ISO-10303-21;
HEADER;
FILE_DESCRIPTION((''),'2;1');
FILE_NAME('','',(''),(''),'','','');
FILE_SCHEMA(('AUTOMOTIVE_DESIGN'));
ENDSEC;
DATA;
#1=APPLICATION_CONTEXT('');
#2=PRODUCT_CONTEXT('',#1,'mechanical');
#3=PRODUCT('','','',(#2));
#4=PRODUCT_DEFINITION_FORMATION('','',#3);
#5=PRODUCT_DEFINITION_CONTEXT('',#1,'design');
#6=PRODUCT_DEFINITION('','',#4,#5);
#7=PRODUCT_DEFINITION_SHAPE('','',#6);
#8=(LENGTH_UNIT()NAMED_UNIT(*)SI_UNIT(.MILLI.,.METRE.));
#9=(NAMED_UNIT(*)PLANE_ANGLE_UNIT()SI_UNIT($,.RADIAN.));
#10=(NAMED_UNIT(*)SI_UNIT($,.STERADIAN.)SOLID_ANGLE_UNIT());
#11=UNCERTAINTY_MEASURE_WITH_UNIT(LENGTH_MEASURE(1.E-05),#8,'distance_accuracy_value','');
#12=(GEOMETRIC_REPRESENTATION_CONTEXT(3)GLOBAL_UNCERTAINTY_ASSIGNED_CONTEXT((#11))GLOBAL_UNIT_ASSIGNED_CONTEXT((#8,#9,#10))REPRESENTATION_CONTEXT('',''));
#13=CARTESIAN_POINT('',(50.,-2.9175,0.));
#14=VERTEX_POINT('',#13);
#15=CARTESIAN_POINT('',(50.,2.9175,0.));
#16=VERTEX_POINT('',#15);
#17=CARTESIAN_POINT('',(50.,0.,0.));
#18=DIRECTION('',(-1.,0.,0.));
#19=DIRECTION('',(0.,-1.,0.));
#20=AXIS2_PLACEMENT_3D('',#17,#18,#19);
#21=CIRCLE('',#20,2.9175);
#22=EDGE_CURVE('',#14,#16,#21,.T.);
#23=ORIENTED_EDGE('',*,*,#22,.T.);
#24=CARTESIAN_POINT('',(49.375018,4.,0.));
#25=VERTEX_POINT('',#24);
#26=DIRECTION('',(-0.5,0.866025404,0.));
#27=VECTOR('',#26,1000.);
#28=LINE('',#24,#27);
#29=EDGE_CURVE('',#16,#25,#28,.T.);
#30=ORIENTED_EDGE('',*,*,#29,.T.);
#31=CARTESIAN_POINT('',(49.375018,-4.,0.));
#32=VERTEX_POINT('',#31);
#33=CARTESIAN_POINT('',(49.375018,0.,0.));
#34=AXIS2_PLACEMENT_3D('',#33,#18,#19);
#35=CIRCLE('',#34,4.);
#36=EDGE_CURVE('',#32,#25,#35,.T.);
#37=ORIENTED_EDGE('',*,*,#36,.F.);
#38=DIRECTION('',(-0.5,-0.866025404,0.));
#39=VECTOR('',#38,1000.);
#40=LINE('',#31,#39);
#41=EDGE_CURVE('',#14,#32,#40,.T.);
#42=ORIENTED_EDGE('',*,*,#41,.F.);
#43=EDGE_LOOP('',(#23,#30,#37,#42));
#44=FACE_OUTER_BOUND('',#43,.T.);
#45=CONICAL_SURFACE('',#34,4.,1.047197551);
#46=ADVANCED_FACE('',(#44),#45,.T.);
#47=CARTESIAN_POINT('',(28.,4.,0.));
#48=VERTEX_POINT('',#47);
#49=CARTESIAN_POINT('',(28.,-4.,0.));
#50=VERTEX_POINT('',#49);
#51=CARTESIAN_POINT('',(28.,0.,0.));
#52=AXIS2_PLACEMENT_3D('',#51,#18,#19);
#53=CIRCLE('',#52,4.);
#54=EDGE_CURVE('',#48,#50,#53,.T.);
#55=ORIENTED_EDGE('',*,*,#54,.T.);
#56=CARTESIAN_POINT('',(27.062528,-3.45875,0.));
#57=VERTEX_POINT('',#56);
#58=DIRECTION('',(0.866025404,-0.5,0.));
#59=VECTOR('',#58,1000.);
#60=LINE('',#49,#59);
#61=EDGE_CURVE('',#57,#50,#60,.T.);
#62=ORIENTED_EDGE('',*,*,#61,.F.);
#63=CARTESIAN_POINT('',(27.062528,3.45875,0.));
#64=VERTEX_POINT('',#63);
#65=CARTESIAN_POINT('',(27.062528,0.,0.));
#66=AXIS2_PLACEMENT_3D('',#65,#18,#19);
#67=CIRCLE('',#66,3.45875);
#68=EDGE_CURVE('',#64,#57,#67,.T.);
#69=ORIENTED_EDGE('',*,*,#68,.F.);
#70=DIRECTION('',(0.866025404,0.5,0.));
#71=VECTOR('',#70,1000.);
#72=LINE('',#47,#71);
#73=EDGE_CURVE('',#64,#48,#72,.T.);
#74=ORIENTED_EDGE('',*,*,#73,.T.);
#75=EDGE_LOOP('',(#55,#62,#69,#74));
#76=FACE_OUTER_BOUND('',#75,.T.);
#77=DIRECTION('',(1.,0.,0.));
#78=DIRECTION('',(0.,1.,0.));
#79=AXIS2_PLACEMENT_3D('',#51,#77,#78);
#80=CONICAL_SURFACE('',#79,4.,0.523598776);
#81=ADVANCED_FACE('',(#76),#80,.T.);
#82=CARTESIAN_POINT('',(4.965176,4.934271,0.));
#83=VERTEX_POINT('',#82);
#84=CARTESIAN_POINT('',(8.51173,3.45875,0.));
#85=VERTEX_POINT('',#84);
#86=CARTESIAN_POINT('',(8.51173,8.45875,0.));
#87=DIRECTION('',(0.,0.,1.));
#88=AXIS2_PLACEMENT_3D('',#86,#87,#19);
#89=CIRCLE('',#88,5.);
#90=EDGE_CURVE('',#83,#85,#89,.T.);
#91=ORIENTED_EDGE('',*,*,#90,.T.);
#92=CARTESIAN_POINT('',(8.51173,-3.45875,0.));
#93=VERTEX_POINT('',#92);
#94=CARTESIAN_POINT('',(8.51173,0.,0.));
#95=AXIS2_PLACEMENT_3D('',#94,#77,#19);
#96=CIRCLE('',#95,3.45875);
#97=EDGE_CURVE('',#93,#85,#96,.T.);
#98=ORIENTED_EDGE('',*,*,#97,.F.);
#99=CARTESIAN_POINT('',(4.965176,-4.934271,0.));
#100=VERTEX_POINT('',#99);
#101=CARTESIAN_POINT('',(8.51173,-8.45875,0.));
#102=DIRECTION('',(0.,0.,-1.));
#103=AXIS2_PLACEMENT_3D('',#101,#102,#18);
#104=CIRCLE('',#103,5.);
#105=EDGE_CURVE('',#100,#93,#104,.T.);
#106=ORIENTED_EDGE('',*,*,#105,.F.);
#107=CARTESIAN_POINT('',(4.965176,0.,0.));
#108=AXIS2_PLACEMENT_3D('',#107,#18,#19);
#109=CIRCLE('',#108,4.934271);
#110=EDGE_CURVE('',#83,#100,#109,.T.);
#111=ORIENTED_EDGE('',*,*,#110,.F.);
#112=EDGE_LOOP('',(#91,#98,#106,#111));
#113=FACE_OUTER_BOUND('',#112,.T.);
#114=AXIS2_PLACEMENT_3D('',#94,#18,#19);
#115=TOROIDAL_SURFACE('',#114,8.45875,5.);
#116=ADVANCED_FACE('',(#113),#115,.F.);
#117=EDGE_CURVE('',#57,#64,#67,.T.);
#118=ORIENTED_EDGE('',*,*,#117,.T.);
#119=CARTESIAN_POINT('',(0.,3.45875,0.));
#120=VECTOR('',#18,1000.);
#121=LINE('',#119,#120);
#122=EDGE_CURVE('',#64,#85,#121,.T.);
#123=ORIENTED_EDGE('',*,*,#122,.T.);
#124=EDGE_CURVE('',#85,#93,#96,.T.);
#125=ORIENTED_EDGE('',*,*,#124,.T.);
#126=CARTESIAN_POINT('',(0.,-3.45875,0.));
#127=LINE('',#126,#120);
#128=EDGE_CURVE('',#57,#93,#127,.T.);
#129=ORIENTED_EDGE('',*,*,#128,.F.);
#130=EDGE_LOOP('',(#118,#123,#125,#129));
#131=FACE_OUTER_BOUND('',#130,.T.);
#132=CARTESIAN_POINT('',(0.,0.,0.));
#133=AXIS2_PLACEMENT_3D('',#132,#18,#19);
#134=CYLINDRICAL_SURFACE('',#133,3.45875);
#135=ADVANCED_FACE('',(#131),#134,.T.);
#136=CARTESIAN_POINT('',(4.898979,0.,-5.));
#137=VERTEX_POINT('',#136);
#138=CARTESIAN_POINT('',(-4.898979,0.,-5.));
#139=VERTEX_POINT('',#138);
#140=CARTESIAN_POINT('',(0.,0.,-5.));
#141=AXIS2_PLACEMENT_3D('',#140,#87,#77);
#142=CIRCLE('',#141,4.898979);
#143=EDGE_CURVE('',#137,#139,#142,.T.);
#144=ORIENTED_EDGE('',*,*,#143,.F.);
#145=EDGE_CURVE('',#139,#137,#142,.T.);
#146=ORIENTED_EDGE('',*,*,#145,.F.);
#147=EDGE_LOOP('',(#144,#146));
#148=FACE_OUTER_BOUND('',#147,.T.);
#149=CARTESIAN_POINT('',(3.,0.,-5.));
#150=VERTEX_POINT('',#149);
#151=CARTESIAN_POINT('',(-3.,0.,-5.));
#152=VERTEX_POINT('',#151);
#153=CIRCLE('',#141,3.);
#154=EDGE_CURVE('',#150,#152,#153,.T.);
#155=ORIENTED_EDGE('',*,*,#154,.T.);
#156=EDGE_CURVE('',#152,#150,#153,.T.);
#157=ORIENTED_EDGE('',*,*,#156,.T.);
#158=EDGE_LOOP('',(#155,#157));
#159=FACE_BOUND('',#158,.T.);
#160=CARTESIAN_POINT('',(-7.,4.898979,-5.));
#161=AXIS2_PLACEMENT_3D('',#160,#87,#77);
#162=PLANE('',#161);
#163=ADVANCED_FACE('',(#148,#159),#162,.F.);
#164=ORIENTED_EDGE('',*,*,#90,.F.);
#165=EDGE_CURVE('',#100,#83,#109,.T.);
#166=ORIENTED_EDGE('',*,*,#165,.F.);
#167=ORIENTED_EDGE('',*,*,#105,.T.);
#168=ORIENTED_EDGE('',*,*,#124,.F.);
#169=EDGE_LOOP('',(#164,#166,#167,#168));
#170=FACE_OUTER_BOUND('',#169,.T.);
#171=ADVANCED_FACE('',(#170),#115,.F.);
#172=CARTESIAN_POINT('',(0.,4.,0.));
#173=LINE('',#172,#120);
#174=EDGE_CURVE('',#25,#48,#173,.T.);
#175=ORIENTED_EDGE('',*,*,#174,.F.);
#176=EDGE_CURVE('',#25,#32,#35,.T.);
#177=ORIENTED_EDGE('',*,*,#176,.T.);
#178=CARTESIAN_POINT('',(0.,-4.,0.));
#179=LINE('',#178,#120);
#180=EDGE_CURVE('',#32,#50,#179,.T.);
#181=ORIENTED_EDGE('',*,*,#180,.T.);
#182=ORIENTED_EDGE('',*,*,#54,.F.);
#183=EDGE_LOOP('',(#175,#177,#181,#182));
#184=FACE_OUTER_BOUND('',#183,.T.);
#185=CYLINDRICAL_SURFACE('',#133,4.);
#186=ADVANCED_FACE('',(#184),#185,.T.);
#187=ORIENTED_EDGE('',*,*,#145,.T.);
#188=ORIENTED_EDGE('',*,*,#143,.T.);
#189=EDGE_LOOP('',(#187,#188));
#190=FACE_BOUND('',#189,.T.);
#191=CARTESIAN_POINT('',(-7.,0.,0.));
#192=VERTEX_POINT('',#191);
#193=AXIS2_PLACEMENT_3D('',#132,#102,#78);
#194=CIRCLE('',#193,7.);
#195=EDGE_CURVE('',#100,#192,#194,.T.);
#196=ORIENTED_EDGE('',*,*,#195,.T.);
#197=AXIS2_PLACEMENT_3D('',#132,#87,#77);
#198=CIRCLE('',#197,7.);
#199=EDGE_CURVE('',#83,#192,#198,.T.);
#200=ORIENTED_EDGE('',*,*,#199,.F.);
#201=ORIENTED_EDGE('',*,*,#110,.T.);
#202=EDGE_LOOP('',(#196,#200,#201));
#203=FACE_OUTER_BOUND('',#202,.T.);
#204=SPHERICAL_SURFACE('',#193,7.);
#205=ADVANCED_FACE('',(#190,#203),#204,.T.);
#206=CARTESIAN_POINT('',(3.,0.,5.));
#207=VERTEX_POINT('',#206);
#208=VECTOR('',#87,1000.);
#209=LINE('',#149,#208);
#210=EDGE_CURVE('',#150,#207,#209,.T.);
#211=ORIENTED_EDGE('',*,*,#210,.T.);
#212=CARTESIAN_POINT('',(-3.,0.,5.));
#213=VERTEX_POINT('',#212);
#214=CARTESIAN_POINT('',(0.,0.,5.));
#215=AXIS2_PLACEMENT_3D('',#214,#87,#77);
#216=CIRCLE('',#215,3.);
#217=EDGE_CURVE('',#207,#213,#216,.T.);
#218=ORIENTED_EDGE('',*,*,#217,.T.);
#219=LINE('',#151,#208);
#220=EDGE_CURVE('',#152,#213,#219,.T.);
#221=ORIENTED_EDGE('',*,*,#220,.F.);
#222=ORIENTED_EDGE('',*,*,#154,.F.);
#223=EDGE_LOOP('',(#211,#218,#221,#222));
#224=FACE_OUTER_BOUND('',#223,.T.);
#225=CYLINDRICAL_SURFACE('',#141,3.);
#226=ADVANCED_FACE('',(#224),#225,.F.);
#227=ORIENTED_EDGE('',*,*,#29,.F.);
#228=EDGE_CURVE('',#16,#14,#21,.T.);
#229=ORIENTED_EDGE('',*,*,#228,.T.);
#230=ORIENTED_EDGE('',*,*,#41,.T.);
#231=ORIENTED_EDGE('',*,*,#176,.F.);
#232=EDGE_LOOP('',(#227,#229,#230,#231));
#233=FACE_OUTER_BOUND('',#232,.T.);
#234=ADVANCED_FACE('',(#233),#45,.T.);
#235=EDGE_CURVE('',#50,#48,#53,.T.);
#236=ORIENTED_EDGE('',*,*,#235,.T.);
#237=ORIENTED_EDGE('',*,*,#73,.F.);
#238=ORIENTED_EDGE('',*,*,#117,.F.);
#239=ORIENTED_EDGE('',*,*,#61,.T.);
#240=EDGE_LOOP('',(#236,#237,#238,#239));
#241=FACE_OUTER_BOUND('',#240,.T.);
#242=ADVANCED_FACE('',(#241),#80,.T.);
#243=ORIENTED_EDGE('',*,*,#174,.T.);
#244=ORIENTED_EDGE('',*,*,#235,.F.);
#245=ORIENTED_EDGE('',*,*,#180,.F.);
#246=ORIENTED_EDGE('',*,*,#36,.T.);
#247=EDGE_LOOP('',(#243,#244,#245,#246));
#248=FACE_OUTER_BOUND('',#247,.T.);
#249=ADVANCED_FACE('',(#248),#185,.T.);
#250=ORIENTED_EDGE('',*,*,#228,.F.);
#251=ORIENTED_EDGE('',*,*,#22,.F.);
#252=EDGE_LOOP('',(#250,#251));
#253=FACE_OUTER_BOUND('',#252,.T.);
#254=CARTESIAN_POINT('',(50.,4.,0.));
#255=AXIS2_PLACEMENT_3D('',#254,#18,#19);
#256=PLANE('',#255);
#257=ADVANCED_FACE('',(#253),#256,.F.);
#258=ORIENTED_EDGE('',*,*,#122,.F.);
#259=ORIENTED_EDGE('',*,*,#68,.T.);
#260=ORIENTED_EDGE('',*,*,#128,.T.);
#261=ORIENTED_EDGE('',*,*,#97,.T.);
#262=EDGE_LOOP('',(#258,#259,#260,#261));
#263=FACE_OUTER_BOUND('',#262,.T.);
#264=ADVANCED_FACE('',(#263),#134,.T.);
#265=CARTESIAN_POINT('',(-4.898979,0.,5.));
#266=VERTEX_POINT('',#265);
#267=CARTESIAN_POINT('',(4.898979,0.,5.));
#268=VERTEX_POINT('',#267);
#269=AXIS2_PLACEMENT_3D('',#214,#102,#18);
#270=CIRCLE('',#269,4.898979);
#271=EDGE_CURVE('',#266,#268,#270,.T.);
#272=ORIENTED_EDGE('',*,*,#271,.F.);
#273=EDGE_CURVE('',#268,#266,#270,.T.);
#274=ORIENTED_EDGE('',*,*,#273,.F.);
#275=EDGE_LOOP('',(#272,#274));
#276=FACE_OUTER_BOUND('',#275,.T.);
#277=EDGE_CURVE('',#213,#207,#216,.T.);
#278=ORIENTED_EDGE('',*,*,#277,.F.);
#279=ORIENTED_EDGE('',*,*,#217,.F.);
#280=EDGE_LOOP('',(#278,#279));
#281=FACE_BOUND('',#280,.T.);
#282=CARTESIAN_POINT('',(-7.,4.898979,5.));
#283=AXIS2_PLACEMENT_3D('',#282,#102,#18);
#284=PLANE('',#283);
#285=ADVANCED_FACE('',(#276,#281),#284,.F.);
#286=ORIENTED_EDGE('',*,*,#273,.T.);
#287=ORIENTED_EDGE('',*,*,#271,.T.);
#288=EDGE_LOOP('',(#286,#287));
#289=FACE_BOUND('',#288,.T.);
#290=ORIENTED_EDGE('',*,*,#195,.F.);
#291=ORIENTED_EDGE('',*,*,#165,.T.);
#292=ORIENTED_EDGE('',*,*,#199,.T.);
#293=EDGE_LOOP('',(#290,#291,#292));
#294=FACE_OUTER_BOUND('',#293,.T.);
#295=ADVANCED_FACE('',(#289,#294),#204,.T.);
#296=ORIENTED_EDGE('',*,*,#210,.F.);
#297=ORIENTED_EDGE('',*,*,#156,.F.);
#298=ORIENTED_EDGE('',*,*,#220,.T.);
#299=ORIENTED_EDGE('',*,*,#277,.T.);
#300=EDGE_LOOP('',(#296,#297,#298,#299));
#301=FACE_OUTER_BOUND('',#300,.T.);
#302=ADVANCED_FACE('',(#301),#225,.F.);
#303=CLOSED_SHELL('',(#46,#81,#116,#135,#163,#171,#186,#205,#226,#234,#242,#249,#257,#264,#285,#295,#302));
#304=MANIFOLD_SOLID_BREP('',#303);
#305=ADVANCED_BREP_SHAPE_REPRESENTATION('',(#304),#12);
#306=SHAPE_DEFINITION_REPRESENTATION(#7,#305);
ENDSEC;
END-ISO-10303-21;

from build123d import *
from build123d.topology import SkipClean

# Parameters (mm, degrees)
CUT_EXTRUDE1_DEPTH      = 13.124356
CUT_EXTRUDE1_DEPTH_BACK = 13.124356
SKETCH4_R               = 3
CUT_EXTRUDE2_DEPTH      = 16.556349
CHAMFER1_SIZE           = 0.4
FILLET1_R               = 5


with BuildPart() as part:
    # Sketch1 → Boss-Revolve (revolve)
    with BuildSketch(Plane.XY):
        with BuildLine():
            Line((-7, 0), (7, 0))
            ThreePointArc((7, 0), (0, 7), (-7, 0))
        make_face()
    revolve(axis=Axis((-13.286843, 0, 0), (1, 0, 0)))

    # Sketch2 → Cut-Extrude1 (cut, two sides: drawn at the far end of the back side and taken through both)
    with SkipClean():  # the faces are left unmerged after this step: merging them gives an invalid solid
        with BuildSketch(Plane(origin=(0, 0, 0), x_dir=(0, 0, -1), z_dir=(1, 0, 0)).offset(-CUT_EXTRUDE1_DEPTH_BACK)):
            with BuildLine():
                Line((-5, 4.898979), (-5, -4.898979))
                ThreePointArc((-5, -4.898979), (-7, 0), (-5, 4.898979))
            make_face()
            with BuildLine():
                Line((5, 4.898979), (5, -4.898979))
                ThreePointArc((5, -4.898979), (7, 0), (5, 4.898979))
            make_face()
        extrude(amount=CUT_EXTRUDE1_DEPTH + CUT_EXTRUDE1_DEPTH_BACK, mode=Mode.SUBTRACT)

    # Sketch4 → Cut-Extrude2 (cut, through all)
    with SkipClean():  # the faces are left unmerged after this step: merging them gives an invalid solid
        with BuildSketch(Plane.XY.offset(5)):
            Circle(SKETCH4_R)
        extrude(amount=-CUT_EXTRUDE2_DEPTH, mode=Mode.SUBTRACT)

    # Sketch5 → Boss-Revolve1 (revolve)
    with SkipClean():  # the faces are left unmerged after this step: merging them gives an invalid solid
        with BuildSketch(Plane.XY, mode=Mode.PRIVATE) as boss_revolve1_sk:
            Polygon((3.469445, 3.45875), (3.469445, 0), (50, 0), (50, 4), (28, 4), (27.062528, 3.45875), align=None)
        revolve(boss_revolve1_sk.sketch.rotate(Axis((0, 0, 0), (1, 0, 0)), 180), axis=Axis((0, 0, 0), (1, 0, 0)))

    # Chamfer1
    chamfer1_edges = [part.edges().sort_by_distance(p)[0] for p in [
        (50, 4, 0),
    ]]
    chamfer(chamfer1_edges, length=CHAMFER1_SIZE)

    # Sketch6 → Cut-Revolve1 (revolve, cut)
    with SkipClean():  # the faces are left unmerged after this step: merging them gives an invalid solid
        with BuildSketch(Plane.XY, mode=Mode.PRIVATE) as cut_revolve1_sk:
            Polygon((49.375018, 4), (50.624982, 4), (50, 2.9175), align=None)
        revolve(cut_revolve1_sk.sketch.rotate(Axis((0, 0, 0), (1, 0, 0)), 180), axis=Axis((0, 0, 0), (1, 0, 0)), mode=Mode.SUBTRACT)

    # Fillet1
    fillet1_edges = [part.edges().sort_by_distance(p)[0] for p in [
        (6.085807, 0, -3.45875),
    ]]
    fillet(fillet1_edges, radius=FILLET1_R)


solid = part.part
